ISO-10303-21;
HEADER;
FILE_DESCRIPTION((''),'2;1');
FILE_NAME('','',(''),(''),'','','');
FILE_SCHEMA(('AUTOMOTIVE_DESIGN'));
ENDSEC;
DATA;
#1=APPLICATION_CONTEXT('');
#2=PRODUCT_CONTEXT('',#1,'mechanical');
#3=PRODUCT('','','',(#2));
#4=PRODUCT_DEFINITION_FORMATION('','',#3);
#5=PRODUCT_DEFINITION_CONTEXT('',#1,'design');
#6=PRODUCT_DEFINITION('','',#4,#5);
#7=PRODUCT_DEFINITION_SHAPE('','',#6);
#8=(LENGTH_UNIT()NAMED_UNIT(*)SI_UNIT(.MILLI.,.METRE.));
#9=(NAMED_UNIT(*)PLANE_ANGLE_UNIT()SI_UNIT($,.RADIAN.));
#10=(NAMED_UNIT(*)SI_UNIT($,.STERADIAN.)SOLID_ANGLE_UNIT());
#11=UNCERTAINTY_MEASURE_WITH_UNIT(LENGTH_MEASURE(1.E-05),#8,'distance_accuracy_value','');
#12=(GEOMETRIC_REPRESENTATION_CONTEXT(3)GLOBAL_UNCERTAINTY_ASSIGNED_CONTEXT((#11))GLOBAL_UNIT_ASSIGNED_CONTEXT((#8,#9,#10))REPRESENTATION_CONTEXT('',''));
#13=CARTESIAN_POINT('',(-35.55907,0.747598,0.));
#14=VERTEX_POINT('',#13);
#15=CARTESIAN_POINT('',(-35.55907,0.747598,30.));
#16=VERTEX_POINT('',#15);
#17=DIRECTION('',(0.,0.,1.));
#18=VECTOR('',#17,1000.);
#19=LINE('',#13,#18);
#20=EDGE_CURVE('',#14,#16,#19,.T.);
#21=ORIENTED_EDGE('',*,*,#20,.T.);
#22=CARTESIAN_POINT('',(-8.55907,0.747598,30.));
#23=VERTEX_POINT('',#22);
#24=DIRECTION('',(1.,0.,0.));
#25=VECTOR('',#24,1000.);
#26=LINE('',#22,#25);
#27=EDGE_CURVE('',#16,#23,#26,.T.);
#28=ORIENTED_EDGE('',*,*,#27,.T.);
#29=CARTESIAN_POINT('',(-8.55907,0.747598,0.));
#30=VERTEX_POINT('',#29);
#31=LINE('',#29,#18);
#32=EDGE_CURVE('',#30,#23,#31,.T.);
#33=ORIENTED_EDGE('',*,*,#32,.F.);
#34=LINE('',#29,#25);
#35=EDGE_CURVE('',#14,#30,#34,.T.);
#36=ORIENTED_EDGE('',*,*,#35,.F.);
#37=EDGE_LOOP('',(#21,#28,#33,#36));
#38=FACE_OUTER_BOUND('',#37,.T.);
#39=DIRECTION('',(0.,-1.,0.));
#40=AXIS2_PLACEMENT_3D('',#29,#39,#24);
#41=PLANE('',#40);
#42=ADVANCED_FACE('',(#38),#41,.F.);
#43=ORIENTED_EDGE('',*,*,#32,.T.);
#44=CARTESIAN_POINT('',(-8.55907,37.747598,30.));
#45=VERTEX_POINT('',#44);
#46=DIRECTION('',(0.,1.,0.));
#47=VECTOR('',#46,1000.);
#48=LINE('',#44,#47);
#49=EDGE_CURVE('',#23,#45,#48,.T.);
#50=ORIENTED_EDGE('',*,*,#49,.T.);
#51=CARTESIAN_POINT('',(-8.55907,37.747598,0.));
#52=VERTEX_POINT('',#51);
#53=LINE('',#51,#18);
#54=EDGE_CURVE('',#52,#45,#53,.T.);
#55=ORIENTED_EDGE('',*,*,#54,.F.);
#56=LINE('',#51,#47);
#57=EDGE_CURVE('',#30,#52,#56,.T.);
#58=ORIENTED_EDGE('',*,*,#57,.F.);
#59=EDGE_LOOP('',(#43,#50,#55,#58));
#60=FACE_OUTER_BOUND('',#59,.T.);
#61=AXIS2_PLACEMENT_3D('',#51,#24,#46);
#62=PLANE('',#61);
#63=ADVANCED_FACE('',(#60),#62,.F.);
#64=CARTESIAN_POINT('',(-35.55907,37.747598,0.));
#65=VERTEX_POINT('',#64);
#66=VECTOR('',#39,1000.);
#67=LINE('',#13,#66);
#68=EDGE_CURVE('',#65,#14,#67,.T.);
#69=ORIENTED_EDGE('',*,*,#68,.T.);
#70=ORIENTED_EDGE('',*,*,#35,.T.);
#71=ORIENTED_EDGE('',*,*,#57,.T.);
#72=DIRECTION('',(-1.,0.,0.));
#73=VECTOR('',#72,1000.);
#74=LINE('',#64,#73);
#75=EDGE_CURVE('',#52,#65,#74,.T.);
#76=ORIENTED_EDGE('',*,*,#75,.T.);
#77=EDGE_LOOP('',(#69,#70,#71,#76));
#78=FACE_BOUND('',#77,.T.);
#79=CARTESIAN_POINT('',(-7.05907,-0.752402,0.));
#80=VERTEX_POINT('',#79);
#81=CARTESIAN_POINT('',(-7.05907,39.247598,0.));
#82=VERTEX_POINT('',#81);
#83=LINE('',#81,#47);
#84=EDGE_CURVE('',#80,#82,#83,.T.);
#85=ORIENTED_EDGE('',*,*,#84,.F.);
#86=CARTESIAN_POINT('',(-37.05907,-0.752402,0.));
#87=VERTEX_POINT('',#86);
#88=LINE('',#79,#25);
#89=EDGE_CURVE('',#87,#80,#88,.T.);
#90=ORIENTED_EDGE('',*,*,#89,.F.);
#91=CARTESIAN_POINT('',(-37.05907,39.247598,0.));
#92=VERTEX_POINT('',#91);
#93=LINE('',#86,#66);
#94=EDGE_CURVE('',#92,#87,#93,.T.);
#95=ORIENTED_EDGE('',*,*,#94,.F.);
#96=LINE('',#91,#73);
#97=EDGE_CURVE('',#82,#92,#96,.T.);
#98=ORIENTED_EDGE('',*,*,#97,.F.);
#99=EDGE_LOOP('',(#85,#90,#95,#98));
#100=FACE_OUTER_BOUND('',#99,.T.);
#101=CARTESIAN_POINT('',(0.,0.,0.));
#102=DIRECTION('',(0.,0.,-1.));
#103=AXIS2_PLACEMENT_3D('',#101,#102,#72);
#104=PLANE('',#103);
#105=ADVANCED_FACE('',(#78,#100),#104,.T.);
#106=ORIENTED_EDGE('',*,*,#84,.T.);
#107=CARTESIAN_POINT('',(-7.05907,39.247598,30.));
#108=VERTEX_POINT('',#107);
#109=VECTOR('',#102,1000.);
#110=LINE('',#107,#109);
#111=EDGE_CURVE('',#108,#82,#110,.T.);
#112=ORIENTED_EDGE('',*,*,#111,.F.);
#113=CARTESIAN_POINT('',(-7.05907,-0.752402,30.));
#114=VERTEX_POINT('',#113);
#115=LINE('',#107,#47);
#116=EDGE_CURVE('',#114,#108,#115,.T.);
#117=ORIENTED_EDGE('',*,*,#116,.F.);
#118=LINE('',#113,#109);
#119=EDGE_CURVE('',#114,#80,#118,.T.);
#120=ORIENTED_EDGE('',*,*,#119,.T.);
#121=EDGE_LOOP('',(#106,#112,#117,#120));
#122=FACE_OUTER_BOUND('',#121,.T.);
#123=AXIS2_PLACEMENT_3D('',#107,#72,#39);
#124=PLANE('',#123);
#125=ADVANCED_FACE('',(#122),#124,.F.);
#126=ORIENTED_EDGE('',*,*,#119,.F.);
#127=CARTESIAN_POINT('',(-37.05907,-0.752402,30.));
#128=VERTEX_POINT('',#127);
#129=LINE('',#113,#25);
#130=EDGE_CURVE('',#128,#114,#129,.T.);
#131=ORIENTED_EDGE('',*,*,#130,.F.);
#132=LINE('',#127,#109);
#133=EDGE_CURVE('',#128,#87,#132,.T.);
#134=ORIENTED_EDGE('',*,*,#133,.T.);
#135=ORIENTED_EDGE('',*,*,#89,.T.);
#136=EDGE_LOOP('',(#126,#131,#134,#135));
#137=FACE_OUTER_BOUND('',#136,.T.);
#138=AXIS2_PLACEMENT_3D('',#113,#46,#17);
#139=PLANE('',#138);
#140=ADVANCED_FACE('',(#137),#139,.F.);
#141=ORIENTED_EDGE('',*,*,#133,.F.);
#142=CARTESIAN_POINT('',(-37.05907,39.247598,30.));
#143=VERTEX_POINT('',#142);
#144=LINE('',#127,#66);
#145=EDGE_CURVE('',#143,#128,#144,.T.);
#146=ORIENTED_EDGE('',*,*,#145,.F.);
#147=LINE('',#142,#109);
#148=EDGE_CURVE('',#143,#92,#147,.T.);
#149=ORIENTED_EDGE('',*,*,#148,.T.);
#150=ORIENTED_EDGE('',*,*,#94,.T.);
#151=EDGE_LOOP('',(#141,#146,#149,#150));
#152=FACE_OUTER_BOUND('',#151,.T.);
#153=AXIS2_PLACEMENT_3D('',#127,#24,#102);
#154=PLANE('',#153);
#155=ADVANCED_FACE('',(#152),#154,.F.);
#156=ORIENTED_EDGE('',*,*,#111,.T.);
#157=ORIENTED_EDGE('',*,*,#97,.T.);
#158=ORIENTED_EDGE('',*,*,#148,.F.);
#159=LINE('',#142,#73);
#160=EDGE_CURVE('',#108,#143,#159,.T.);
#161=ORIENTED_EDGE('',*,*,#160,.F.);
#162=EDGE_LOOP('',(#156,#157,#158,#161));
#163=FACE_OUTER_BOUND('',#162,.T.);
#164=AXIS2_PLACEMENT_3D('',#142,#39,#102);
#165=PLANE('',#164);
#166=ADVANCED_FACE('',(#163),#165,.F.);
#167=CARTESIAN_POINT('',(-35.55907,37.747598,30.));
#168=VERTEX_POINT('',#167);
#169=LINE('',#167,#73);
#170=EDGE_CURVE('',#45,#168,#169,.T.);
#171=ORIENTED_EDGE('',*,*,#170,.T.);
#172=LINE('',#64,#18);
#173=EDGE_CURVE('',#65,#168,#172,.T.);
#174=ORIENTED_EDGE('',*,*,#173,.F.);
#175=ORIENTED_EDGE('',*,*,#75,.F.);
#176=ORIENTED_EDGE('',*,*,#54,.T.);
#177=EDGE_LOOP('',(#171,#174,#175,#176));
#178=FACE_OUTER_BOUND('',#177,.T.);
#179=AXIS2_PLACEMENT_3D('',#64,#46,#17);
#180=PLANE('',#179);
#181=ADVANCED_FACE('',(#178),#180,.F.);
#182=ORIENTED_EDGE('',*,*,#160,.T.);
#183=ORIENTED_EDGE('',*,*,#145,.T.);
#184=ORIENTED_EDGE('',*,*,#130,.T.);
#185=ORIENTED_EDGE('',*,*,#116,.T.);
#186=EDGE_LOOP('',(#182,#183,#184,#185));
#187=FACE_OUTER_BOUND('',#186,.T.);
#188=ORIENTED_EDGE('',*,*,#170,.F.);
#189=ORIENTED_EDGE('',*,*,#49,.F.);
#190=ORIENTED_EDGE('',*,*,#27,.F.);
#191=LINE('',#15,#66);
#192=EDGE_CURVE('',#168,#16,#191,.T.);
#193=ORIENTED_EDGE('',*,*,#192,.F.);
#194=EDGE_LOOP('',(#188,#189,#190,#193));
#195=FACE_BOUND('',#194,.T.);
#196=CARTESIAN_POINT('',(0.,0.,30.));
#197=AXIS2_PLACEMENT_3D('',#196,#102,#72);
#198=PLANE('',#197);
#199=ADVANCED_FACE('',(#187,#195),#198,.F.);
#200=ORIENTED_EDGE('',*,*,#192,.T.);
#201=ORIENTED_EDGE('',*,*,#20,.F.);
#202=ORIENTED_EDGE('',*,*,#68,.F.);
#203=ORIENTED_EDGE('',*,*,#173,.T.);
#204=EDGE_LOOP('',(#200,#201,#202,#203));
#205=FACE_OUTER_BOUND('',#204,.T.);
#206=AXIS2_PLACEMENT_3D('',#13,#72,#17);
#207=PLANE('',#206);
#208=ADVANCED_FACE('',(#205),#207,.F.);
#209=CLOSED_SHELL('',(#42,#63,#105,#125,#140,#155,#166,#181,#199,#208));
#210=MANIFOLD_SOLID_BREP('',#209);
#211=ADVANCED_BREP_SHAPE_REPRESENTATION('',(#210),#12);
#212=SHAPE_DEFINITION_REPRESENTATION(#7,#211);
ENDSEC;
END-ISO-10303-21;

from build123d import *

# Parameters (mm, degrees)
SKETCH1_W           = 30
SKETCH1_H           = 40
BOSS_EXTRUDE1_DEPTH = 30
SKETCH2_W           = 27
SKETCH2_H           = 37
CUT_EXTRUDE1_DEPTH  = 62.755555196


with BuildPart() as part:
    # Sketch1 → Boss-Extrude1 (new body)
    with BuildSketch(Plane.XY):
        with Locations((-22.059069992, 19.247597747)):
            Rectangle(SKETCH1_W, SKETCH1_H)
    extrude(amount=BOSS_EXTRUDE1_DEPTH)

    # Sketch2 → Cut-Extrude1 (cut, through all)
    with BuildSketch(Plane.XY.offset(30)):
        with Locations((-22.059069992, 19.247597747)):
            Rectangle(SKETCH2_W, SKETCH2_H)
    extrude(amount=-CUT_EXTRUDE1_DEPTH, mode=Mode.SUBTRACT)


solid = part.part
